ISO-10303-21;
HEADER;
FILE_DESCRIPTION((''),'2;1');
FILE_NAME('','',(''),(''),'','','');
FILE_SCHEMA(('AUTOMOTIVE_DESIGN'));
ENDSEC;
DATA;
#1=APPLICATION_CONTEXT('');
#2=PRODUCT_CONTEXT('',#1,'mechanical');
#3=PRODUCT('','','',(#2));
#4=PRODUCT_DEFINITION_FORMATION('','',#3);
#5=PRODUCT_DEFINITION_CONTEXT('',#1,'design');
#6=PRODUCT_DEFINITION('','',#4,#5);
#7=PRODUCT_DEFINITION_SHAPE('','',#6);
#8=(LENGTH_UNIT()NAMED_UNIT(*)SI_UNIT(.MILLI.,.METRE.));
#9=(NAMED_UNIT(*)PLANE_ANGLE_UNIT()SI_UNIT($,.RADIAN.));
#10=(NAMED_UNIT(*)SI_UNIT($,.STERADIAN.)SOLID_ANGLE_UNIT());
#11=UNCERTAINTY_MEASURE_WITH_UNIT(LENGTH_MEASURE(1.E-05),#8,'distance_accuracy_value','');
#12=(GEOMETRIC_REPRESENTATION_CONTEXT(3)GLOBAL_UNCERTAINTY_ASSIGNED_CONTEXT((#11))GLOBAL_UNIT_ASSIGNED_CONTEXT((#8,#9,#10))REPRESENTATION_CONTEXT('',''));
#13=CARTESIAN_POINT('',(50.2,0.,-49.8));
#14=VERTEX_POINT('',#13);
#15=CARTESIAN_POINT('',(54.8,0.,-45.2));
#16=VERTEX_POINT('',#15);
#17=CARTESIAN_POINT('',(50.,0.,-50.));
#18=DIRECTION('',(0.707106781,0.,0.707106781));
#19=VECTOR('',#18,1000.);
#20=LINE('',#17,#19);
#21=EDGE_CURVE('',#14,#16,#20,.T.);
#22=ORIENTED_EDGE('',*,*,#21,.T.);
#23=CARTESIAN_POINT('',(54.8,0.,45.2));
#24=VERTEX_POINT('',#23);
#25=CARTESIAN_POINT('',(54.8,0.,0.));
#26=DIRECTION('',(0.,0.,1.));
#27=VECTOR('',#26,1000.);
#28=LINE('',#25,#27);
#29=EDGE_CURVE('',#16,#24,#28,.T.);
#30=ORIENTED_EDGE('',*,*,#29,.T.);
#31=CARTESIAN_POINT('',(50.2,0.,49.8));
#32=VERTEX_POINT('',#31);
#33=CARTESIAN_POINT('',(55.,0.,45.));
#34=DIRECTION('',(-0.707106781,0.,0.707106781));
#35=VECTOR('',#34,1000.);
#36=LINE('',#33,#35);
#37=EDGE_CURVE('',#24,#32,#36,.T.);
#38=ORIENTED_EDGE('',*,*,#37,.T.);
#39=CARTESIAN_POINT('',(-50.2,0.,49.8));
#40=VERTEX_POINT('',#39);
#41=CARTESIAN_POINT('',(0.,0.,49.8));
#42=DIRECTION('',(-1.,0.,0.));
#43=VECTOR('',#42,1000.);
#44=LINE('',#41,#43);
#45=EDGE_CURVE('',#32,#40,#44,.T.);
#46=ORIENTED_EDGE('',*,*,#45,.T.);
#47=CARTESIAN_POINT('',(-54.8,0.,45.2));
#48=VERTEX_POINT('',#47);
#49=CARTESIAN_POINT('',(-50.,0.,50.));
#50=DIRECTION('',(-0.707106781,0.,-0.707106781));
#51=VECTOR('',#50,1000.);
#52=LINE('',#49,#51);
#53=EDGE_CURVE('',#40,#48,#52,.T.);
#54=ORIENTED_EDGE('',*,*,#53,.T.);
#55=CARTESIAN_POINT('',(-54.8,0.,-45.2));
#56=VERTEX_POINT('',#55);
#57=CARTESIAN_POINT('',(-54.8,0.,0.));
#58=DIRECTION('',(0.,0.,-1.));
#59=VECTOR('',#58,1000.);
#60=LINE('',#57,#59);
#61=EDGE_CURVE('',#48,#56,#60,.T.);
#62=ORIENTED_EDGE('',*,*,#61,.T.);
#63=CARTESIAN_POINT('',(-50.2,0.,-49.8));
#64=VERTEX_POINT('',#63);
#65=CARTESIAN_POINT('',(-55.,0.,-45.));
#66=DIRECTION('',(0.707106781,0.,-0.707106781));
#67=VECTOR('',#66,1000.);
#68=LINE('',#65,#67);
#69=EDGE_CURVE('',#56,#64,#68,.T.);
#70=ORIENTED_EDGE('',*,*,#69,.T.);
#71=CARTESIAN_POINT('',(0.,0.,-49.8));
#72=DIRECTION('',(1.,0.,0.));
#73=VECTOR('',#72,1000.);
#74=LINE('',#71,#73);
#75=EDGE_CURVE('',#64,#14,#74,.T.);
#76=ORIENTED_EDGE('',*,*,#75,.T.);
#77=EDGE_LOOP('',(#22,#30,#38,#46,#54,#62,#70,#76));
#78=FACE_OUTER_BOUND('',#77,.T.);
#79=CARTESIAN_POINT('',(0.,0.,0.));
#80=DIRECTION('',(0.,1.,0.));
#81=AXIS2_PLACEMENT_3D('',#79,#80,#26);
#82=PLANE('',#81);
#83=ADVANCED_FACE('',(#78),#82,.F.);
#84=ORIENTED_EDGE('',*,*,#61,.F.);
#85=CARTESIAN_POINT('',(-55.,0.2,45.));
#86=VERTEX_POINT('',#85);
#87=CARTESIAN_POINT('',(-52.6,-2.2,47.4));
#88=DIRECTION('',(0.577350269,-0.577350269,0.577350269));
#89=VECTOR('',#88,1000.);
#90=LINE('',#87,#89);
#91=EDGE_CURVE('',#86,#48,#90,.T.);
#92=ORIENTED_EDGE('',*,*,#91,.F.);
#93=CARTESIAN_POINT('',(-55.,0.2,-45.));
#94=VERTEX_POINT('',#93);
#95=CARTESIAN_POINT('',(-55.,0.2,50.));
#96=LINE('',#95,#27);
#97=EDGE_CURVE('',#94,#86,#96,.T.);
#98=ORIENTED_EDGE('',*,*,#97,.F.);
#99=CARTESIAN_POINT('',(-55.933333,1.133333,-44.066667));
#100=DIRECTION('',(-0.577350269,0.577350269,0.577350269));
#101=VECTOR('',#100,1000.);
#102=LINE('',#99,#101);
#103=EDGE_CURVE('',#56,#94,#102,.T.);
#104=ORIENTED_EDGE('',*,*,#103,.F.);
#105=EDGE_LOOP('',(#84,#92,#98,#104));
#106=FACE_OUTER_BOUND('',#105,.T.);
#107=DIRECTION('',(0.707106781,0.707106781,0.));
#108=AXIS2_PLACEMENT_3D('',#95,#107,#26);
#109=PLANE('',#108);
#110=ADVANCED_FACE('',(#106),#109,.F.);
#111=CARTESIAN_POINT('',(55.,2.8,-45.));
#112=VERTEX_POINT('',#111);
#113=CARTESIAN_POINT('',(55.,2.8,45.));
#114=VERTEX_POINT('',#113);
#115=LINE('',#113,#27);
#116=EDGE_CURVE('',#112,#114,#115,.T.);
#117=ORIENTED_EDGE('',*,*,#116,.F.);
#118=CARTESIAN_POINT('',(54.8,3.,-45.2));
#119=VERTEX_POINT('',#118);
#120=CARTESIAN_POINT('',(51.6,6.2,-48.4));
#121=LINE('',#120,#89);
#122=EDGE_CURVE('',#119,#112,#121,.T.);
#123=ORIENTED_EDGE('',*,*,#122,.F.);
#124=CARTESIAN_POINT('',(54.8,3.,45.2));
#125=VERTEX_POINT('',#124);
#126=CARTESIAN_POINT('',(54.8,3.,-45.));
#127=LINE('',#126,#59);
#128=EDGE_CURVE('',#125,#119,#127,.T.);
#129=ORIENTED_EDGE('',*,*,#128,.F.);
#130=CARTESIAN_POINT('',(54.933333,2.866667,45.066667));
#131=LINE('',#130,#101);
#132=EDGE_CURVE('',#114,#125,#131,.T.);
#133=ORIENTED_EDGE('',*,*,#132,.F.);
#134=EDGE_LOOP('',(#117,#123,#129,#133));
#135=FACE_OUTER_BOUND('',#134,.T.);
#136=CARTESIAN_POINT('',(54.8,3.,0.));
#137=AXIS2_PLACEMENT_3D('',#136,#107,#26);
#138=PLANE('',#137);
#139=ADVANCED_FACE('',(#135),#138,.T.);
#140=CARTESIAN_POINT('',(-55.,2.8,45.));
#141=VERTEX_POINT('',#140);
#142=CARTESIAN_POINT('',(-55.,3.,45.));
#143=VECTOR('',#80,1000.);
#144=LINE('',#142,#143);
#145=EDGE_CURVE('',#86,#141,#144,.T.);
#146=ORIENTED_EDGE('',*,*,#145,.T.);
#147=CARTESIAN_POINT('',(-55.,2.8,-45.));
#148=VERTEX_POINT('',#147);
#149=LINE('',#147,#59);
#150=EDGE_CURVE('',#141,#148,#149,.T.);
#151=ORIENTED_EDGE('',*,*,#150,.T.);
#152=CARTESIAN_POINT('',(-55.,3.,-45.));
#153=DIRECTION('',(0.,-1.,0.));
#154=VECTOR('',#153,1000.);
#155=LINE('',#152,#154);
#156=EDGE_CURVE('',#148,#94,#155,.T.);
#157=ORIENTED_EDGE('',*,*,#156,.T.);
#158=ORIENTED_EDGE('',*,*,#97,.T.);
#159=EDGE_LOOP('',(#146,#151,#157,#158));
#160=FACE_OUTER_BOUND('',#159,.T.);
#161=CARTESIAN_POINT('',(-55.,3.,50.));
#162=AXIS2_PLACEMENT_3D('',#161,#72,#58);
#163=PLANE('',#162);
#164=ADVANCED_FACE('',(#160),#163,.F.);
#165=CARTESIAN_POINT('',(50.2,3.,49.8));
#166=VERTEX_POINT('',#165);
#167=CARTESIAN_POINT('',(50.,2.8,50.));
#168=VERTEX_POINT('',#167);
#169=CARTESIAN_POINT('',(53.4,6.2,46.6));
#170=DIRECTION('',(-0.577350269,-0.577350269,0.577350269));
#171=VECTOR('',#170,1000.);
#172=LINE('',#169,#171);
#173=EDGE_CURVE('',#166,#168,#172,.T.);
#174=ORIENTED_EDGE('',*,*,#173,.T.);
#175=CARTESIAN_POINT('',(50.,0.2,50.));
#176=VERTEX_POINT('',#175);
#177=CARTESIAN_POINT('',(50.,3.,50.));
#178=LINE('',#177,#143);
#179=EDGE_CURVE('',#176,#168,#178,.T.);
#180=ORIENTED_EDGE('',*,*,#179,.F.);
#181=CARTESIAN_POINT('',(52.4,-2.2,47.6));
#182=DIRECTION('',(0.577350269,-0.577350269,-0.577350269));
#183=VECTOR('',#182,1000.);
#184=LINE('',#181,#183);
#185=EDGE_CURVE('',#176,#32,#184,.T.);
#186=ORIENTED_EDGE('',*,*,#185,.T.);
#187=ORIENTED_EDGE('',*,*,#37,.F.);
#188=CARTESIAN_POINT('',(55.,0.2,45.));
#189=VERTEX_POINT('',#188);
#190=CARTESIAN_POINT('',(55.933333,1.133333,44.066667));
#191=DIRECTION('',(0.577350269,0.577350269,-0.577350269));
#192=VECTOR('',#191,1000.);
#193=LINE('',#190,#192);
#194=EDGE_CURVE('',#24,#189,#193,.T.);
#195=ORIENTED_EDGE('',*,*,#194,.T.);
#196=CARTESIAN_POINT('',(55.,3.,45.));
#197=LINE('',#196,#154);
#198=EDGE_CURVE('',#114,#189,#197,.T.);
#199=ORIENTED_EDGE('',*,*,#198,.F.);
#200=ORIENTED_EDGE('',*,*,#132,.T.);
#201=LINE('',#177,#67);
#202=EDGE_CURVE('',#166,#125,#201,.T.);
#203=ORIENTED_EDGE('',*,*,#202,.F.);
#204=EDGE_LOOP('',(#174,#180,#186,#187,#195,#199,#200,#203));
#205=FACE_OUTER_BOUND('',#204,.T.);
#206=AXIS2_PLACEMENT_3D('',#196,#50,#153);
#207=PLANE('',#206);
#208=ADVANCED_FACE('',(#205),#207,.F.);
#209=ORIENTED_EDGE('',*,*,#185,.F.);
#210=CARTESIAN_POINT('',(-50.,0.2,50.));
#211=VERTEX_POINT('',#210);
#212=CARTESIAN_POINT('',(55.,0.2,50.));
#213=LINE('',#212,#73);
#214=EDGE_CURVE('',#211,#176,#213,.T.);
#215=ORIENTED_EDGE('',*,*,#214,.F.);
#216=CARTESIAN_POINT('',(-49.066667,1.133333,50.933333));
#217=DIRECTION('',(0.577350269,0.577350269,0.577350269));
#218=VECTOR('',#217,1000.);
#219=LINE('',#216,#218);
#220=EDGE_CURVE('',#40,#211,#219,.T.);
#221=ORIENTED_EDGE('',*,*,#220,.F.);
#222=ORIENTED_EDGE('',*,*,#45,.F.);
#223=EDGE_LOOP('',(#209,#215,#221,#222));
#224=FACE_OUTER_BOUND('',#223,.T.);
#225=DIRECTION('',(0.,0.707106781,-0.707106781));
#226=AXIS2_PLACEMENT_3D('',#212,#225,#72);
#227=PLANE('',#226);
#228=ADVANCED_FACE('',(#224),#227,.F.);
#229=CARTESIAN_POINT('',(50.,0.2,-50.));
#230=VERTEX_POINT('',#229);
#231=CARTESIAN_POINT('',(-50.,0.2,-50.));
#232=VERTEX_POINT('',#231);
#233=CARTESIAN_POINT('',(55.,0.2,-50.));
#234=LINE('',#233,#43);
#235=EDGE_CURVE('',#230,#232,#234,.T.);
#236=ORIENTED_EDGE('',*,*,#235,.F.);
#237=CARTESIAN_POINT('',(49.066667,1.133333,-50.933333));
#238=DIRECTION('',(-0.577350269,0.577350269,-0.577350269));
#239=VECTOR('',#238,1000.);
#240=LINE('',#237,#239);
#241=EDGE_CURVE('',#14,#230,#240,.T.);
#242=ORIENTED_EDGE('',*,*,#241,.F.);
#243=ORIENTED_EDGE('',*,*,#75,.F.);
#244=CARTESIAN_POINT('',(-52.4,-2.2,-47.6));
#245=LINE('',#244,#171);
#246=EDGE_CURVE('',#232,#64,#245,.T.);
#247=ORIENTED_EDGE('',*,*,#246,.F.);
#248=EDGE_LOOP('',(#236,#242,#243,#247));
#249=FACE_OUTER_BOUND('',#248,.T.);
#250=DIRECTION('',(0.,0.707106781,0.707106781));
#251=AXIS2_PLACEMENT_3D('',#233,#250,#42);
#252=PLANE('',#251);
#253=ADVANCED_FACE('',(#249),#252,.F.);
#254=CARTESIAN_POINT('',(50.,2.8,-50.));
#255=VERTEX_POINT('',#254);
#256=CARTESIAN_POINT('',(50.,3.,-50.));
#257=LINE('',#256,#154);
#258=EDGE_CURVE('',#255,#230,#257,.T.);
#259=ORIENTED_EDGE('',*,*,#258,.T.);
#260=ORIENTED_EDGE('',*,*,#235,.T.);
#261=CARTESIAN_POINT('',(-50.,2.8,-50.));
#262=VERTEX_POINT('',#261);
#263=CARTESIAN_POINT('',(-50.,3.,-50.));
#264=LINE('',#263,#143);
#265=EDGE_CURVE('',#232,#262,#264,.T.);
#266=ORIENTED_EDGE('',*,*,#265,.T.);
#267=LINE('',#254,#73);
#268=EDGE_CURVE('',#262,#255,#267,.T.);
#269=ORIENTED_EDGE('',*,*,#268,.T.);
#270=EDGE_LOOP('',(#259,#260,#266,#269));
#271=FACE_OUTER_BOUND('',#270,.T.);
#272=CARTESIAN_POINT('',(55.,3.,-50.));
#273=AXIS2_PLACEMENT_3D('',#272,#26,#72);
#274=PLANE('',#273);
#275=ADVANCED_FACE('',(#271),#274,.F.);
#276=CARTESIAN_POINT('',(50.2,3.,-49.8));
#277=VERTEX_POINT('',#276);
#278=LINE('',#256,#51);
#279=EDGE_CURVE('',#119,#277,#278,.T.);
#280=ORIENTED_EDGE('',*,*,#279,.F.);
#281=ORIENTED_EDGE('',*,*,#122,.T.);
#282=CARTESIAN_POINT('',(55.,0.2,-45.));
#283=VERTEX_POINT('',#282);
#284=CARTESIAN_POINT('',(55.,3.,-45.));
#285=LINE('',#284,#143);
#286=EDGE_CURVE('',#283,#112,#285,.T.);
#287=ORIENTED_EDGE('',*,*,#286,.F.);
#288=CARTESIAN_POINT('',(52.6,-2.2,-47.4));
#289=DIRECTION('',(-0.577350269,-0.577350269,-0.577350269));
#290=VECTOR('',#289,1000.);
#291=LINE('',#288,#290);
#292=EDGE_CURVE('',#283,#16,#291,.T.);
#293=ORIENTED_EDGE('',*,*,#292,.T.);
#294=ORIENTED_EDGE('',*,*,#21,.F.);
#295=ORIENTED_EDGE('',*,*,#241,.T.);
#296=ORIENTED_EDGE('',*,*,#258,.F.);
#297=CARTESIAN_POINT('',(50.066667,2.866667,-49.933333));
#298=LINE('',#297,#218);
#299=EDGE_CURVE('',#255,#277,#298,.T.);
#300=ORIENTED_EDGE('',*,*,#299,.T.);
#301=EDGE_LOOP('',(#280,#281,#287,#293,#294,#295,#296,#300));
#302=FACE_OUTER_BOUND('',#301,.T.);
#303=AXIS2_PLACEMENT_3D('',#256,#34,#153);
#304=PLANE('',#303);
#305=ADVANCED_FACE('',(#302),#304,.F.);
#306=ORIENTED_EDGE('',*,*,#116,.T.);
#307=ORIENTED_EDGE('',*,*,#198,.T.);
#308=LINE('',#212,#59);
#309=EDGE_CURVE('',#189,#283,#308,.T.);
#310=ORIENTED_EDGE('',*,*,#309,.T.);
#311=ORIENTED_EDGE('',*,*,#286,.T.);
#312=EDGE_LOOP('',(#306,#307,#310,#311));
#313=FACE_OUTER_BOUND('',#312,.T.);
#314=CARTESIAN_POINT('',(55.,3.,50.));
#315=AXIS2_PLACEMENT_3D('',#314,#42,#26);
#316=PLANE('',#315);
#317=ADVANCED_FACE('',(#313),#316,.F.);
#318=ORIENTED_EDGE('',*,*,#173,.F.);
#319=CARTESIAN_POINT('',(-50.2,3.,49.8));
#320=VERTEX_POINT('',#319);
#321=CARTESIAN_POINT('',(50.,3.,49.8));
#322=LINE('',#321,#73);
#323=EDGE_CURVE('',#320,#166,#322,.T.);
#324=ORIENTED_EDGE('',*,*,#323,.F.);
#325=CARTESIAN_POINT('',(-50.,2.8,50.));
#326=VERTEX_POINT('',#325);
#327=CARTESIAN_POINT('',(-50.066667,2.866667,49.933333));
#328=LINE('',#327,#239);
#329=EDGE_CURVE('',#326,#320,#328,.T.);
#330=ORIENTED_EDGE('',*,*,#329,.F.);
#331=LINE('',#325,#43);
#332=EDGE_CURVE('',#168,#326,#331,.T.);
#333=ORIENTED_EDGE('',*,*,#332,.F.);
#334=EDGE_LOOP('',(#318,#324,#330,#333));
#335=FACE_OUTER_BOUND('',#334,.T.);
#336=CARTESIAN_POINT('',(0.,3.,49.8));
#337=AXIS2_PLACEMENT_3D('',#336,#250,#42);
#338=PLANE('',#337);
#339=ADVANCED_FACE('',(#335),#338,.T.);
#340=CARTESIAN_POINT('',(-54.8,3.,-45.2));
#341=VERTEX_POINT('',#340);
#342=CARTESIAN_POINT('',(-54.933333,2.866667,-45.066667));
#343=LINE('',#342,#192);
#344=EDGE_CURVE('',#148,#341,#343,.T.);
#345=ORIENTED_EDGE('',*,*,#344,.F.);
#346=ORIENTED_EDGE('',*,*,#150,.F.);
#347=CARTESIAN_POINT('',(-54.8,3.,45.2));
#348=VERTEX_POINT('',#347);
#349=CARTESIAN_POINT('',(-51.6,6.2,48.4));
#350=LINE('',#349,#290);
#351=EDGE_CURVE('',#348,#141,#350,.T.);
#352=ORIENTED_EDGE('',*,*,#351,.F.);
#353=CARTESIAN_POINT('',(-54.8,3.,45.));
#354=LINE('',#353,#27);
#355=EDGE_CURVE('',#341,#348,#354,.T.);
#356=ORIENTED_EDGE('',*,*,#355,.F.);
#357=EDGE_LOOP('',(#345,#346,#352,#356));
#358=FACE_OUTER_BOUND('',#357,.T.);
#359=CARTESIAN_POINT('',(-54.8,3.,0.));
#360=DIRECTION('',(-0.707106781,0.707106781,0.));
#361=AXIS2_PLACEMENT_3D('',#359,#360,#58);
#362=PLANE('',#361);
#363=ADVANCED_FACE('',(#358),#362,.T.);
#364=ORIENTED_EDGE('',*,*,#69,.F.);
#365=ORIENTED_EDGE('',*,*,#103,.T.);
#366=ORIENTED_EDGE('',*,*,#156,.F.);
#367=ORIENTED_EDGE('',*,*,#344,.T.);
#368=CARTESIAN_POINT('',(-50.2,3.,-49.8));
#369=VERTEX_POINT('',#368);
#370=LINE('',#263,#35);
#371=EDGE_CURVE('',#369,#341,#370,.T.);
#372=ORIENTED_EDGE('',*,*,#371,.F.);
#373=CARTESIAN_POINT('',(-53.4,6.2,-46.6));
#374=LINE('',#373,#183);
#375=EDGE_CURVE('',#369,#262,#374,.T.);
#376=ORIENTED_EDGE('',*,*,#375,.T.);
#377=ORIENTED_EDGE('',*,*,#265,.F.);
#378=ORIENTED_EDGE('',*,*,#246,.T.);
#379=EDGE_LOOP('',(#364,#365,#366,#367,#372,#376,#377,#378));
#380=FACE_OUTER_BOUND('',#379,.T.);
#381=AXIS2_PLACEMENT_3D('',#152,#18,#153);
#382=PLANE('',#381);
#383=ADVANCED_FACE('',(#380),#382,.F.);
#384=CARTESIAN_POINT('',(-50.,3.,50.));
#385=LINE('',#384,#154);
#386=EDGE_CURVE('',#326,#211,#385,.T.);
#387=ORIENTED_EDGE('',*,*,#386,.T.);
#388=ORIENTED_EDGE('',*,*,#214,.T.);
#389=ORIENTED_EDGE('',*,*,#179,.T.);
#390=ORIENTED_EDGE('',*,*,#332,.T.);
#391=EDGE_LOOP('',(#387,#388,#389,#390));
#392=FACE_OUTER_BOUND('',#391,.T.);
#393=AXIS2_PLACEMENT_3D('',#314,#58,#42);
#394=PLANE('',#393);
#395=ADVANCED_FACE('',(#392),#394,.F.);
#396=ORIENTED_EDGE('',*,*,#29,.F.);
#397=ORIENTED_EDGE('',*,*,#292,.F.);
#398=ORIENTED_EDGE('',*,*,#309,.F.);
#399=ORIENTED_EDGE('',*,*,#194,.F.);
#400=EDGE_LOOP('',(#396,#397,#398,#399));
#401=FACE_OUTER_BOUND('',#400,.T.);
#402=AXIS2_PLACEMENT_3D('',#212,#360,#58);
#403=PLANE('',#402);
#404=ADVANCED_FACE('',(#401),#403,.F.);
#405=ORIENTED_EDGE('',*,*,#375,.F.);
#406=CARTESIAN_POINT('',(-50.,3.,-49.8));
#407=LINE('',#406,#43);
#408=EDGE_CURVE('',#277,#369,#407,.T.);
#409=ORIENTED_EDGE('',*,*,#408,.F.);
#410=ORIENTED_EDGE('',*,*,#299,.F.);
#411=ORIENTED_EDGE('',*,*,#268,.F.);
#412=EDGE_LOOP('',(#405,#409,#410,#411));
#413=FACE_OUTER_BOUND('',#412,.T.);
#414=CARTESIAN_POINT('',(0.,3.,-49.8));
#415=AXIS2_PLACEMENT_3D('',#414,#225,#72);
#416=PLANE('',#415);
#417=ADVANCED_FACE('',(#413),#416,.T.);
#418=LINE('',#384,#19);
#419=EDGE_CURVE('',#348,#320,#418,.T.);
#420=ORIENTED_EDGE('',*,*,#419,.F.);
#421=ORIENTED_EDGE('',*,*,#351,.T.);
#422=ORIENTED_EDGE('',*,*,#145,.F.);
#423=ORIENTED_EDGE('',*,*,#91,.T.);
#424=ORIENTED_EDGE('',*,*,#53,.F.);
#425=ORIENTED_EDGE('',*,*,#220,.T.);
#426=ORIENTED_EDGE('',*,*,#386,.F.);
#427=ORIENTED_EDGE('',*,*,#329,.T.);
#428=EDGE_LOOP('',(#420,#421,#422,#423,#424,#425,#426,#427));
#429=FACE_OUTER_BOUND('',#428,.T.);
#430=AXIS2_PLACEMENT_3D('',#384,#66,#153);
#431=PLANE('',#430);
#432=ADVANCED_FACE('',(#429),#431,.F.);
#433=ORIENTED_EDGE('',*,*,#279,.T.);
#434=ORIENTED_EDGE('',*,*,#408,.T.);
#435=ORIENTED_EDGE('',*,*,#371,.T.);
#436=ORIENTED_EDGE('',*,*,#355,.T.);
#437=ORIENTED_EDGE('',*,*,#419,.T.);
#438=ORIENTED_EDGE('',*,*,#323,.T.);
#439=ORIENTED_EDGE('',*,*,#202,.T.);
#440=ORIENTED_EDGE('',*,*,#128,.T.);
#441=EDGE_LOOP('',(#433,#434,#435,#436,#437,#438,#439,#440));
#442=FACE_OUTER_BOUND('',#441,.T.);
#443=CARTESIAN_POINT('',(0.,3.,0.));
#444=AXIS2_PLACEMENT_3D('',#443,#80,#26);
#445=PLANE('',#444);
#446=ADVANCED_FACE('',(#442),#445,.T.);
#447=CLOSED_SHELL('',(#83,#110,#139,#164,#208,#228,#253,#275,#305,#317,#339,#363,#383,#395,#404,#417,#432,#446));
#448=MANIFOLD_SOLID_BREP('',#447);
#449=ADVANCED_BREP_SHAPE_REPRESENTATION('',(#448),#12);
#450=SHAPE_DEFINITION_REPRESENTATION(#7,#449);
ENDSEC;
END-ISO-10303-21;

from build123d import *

# Parameters (mm, degrees)
SKETCH1_W      = 110
SKETCH1_H      = 100
EXTRUDE1_DEPTH = 3
CHAMFER1_SIZE  = 5
CHAMFER2_SIZE  = 0.2


with BuildPart() as part:
    # Sketch1 → Extrude1 (new body)
    with BuildSketch(Plane(origin=(0, 0, 0), x_dir=(1, 0, 0), z_dir=(0, 1, 0))):
        Rectangle(SKETCH1_W, SKETCH1_H)
    extrude(amount=EXTRUDE1_DEPTH)

    # Chamfer1
    chamfer1_edges = [part.edges().sort_by_distance(p)[0] for p in [
        (-55, 1.5, -50),
        (55, 1.5, -50),
        (55, 1.5, 50),
        (-55, 1.5, 50),
    ]]
    chamfer(chamfer1_edges, length=CHAMFER1_SIZE)

    # Chamfer2
    chamfer2_edges = [part.edges().sort_by_distance(p)[0] for p in [
        (0, 0, 50),
        (0, 3, 50),
        (-55, 0, 0),
        (0, 0, -50),
        (55, 0, 0),
        (-55, 3, 0),
        (55, 3, 0),
        (0, 3, -50),
    ]]
    chamfer(chamfer2_edges, length=CHAMFER2_SIZE)


solid = part.part
